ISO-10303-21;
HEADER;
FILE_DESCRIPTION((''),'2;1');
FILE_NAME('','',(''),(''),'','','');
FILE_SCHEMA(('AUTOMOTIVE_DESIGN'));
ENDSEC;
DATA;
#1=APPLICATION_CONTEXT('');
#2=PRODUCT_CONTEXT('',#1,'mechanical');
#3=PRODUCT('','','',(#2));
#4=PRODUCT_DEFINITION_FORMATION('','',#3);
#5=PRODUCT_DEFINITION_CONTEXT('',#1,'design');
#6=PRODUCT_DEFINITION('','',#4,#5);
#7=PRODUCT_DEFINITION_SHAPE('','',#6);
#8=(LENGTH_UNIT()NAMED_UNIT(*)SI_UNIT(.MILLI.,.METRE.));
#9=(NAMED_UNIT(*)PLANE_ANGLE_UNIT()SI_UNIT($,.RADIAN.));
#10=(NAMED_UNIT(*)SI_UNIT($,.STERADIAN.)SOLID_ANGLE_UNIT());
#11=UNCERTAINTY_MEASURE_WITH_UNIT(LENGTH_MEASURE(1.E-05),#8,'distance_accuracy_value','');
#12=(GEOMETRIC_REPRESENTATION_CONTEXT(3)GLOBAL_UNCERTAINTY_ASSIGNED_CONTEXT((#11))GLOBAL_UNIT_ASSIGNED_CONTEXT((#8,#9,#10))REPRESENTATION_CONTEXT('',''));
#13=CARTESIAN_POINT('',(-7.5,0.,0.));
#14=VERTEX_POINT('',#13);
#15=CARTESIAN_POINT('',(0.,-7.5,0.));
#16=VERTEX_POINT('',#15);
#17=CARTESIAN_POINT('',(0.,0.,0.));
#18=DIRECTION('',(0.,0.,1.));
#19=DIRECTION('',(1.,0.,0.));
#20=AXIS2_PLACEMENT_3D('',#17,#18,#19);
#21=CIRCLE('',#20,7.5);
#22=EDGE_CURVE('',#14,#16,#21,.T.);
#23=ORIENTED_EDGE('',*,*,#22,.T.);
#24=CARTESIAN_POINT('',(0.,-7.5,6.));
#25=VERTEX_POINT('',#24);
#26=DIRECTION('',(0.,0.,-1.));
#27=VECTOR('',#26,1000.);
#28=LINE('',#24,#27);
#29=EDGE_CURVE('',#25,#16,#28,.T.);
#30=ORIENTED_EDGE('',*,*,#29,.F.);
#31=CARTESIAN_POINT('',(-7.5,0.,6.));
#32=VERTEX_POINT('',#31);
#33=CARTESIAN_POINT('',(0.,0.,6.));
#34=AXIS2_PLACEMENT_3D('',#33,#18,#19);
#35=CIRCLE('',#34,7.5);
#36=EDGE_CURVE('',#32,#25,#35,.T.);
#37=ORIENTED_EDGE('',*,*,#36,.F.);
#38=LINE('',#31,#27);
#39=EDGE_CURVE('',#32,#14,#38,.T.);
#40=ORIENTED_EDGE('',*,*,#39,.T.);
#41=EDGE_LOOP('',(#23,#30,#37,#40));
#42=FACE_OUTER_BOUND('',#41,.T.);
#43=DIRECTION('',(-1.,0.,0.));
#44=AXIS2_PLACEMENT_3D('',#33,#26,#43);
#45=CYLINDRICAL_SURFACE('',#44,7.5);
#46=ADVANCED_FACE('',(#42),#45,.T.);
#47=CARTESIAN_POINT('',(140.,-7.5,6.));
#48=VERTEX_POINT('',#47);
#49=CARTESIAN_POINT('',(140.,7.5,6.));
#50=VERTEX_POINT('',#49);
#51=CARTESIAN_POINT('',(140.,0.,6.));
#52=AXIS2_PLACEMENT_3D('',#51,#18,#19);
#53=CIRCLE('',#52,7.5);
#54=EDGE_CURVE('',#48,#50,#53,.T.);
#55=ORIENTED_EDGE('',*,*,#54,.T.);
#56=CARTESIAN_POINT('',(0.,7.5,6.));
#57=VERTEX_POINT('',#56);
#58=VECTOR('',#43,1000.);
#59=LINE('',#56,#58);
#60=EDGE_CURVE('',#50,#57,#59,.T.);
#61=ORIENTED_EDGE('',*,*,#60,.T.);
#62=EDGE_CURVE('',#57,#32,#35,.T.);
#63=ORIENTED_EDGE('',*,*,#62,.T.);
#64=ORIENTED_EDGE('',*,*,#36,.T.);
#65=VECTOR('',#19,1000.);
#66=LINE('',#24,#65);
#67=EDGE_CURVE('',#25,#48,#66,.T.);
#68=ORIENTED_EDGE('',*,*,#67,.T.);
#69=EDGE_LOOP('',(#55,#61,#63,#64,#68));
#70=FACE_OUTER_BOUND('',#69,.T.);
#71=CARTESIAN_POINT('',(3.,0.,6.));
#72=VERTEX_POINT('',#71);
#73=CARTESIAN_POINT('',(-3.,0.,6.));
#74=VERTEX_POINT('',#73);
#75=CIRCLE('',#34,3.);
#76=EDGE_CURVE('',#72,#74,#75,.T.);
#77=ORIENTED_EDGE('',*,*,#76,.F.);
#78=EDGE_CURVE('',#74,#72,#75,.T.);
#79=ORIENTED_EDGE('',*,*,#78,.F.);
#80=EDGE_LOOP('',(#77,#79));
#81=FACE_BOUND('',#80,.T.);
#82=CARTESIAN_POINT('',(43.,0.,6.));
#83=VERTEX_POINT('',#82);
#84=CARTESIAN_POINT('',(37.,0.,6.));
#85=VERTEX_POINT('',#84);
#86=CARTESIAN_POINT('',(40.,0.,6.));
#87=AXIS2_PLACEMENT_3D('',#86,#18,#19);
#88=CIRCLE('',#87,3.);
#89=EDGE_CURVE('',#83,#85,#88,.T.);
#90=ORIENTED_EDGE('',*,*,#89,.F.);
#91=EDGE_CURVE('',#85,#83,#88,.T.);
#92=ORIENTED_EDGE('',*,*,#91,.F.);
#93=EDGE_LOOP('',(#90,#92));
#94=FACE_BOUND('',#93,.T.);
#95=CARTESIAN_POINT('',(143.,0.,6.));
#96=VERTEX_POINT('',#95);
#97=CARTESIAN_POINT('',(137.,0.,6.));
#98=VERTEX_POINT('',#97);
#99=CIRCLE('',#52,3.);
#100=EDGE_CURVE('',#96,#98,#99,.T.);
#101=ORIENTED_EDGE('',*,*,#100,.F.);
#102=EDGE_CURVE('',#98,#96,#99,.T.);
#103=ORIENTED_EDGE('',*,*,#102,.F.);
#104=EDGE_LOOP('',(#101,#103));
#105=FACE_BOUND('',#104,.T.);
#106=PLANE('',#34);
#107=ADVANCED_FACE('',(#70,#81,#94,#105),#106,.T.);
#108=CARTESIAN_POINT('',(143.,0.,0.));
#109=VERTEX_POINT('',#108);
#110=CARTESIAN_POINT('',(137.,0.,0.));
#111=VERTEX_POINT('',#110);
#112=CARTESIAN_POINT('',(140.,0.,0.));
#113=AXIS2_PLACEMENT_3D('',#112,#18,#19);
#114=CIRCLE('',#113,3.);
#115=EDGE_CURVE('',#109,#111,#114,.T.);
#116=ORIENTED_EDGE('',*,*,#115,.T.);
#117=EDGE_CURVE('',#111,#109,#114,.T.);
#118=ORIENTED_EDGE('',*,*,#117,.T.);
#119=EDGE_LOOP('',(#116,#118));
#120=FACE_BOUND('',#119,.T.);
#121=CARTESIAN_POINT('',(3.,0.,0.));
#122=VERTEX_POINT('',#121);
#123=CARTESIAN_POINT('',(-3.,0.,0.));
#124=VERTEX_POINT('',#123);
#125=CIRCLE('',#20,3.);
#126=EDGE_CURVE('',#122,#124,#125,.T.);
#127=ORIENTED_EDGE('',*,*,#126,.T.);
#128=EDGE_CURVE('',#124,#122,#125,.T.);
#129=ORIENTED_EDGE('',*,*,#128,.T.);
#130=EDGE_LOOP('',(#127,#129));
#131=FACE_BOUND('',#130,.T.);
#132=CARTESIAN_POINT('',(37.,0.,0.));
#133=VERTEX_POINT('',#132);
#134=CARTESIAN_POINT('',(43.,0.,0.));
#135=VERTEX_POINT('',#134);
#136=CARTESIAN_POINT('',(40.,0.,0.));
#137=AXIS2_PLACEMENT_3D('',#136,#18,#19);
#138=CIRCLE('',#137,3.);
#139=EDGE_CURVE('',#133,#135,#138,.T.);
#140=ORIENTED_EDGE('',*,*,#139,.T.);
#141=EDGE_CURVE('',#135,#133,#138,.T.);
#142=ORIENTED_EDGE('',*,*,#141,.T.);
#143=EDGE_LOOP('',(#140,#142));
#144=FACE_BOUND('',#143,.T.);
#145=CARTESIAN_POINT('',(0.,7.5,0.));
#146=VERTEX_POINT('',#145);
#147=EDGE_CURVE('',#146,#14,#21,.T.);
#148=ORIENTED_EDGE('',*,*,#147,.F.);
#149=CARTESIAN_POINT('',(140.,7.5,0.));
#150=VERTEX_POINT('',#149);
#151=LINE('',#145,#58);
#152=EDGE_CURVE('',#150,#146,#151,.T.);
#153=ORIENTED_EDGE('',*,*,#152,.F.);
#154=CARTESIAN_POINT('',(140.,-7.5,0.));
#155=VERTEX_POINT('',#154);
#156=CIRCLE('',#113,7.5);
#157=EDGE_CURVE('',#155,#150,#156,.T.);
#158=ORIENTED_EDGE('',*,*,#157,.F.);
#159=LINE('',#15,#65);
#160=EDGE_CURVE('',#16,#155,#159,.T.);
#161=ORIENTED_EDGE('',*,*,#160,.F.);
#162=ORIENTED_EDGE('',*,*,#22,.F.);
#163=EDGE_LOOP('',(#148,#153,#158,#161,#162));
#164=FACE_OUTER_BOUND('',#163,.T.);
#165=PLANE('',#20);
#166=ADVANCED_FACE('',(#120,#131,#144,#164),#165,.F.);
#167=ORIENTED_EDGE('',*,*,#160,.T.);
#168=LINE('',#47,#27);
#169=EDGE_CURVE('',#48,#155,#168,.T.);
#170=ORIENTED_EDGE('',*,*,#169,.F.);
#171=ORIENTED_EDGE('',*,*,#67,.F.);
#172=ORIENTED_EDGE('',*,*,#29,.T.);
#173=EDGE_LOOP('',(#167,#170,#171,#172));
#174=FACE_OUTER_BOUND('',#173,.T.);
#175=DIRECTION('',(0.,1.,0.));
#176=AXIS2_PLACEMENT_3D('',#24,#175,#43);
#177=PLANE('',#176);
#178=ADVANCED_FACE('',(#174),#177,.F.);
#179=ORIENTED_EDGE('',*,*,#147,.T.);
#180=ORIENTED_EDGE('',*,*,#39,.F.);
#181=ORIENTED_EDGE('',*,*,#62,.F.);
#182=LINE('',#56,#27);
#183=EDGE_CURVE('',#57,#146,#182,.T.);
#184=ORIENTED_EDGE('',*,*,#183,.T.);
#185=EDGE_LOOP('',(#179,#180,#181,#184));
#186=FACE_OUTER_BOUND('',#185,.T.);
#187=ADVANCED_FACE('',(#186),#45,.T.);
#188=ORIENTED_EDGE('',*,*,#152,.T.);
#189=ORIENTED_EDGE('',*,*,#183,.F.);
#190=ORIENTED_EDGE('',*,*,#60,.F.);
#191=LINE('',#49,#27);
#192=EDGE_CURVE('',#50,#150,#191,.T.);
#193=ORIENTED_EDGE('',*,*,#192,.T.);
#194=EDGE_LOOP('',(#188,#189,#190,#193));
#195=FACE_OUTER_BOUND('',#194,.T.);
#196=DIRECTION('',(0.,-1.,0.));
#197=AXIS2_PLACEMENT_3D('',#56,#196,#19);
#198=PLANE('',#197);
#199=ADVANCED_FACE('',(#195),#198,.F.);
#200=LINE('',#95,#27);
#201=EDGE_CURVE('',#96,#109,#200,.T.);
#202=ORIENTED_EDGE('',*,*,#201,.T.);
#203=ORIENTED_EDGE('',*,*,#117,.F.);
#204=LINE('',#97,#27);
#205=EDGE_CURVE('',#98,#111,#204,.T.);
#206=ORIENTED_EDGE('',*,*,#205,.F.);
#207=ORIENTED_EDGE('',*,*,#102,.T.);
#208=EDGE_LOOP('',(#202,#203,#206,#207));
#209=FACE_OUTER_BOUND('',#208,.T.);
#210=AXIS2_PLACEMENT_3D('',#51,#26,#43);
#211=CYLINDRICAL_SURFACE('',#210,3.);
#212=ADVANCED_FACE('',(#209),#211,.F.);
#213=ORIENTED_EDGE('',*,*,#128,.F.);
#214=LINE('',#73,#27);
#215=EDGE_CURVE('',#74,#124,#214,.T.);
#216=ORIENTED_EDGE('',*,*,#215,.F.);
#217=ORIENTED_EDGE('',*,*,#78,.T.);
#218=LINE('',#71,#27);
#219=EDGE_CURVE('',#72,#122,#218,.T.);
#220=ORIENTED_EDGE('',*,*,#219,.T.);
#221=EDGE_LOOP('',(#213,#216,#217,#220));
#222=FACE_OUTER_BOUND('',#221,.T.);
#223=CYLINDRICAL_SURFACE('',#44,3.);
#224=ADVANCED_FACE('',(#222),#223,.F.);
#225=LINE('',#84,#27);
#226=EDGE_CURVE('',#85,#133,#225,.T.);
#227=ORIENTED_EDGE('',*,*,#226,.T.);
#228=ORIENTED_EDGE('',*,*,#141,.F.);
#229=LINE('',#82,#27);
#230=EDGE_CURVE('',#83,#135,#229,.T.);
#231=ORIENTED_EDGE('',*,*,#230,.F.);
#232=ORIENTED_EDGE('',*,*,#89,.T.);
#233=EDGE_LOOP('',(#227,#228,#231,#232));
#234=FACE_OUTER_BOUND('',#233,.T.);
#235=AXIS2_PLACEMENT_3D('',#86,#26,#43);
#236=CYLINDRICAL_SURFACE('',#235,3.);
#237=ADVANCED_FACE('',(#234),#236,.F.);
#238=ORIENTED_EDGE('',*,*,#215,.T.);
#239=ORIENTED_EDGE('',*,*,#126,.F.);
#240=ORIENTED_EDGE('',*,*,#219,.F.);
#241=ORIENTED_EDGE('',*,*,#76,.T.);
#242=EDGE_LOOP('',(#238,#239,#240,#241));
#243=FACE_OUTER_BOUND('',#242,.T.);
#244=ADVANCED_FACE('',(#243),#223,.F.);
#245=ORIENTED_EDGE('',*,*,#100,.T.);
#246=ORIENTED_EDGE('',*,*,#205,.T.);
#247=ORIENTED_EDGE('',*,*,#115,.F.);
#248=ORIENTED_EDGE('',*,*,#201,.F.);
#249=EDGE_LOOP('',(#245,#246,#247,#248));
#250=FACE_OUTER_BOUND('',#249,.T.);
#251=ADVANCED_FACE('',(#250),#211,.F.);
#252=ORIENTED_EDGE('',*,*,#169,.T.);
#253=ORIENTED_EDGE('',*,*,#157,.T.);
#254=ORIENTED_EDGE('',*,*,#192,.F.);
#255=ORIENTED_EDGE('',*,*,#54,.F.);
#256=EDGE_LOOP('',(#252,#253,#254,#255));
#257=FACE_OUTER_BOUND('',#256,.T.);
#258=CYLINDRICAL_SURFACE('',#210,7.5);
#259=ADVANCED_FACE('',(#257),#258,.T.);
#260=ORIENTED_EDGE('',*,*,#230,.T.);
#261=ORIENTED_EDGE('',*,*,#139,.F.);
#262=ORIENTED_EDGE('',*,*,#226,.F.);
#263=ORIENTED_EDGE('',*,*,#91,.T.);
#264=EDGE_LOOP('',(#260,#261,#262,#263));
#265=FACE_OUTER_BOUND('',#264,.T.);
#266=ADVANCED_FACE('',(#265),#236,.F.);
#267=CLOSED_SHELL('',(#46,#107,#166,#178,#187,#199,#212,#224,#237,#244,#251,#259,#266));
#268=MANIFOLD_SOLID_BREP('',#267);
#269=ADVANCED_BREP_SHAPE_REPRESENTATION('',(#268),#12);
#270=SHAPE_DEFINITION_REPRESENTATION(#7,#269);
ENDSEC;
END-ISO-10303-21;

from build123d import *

# Parameters (mm, degrees)
SKETCH1_R           = 3
BOSS_EXTRUDE1_DEPTH = 6


with BuildPart() as part:
    # Sketch1 → Boss-Extrude1 (new body)
    with BuildSketch(Plane.XY):
        with BuildLine():
            Line((0, 7.5), (140, 7.5))
            ThreePointArc((140, 7.5), (147.5, 0), (140, -7.5))
            Line((140, -7.5), (0, -7.5))
            ThreePointArc((0, -7.5), (-7.5, 0), (0, 7.5))
        make_face()
        Circle(SKETCH1_R, mode=Mode.SUBTRACT)
        with Locations((40, 0)):
            Circle(SKETCH1_R, mode=Mode.SUBTRACT)
        with Locations((140, 0)):
            Circle(SKETCH1_R, mode=Mode.SUBTRACT)
    extrude(amount=BOSS_EXTRUDE1_DEPTH)


solid = part.part
